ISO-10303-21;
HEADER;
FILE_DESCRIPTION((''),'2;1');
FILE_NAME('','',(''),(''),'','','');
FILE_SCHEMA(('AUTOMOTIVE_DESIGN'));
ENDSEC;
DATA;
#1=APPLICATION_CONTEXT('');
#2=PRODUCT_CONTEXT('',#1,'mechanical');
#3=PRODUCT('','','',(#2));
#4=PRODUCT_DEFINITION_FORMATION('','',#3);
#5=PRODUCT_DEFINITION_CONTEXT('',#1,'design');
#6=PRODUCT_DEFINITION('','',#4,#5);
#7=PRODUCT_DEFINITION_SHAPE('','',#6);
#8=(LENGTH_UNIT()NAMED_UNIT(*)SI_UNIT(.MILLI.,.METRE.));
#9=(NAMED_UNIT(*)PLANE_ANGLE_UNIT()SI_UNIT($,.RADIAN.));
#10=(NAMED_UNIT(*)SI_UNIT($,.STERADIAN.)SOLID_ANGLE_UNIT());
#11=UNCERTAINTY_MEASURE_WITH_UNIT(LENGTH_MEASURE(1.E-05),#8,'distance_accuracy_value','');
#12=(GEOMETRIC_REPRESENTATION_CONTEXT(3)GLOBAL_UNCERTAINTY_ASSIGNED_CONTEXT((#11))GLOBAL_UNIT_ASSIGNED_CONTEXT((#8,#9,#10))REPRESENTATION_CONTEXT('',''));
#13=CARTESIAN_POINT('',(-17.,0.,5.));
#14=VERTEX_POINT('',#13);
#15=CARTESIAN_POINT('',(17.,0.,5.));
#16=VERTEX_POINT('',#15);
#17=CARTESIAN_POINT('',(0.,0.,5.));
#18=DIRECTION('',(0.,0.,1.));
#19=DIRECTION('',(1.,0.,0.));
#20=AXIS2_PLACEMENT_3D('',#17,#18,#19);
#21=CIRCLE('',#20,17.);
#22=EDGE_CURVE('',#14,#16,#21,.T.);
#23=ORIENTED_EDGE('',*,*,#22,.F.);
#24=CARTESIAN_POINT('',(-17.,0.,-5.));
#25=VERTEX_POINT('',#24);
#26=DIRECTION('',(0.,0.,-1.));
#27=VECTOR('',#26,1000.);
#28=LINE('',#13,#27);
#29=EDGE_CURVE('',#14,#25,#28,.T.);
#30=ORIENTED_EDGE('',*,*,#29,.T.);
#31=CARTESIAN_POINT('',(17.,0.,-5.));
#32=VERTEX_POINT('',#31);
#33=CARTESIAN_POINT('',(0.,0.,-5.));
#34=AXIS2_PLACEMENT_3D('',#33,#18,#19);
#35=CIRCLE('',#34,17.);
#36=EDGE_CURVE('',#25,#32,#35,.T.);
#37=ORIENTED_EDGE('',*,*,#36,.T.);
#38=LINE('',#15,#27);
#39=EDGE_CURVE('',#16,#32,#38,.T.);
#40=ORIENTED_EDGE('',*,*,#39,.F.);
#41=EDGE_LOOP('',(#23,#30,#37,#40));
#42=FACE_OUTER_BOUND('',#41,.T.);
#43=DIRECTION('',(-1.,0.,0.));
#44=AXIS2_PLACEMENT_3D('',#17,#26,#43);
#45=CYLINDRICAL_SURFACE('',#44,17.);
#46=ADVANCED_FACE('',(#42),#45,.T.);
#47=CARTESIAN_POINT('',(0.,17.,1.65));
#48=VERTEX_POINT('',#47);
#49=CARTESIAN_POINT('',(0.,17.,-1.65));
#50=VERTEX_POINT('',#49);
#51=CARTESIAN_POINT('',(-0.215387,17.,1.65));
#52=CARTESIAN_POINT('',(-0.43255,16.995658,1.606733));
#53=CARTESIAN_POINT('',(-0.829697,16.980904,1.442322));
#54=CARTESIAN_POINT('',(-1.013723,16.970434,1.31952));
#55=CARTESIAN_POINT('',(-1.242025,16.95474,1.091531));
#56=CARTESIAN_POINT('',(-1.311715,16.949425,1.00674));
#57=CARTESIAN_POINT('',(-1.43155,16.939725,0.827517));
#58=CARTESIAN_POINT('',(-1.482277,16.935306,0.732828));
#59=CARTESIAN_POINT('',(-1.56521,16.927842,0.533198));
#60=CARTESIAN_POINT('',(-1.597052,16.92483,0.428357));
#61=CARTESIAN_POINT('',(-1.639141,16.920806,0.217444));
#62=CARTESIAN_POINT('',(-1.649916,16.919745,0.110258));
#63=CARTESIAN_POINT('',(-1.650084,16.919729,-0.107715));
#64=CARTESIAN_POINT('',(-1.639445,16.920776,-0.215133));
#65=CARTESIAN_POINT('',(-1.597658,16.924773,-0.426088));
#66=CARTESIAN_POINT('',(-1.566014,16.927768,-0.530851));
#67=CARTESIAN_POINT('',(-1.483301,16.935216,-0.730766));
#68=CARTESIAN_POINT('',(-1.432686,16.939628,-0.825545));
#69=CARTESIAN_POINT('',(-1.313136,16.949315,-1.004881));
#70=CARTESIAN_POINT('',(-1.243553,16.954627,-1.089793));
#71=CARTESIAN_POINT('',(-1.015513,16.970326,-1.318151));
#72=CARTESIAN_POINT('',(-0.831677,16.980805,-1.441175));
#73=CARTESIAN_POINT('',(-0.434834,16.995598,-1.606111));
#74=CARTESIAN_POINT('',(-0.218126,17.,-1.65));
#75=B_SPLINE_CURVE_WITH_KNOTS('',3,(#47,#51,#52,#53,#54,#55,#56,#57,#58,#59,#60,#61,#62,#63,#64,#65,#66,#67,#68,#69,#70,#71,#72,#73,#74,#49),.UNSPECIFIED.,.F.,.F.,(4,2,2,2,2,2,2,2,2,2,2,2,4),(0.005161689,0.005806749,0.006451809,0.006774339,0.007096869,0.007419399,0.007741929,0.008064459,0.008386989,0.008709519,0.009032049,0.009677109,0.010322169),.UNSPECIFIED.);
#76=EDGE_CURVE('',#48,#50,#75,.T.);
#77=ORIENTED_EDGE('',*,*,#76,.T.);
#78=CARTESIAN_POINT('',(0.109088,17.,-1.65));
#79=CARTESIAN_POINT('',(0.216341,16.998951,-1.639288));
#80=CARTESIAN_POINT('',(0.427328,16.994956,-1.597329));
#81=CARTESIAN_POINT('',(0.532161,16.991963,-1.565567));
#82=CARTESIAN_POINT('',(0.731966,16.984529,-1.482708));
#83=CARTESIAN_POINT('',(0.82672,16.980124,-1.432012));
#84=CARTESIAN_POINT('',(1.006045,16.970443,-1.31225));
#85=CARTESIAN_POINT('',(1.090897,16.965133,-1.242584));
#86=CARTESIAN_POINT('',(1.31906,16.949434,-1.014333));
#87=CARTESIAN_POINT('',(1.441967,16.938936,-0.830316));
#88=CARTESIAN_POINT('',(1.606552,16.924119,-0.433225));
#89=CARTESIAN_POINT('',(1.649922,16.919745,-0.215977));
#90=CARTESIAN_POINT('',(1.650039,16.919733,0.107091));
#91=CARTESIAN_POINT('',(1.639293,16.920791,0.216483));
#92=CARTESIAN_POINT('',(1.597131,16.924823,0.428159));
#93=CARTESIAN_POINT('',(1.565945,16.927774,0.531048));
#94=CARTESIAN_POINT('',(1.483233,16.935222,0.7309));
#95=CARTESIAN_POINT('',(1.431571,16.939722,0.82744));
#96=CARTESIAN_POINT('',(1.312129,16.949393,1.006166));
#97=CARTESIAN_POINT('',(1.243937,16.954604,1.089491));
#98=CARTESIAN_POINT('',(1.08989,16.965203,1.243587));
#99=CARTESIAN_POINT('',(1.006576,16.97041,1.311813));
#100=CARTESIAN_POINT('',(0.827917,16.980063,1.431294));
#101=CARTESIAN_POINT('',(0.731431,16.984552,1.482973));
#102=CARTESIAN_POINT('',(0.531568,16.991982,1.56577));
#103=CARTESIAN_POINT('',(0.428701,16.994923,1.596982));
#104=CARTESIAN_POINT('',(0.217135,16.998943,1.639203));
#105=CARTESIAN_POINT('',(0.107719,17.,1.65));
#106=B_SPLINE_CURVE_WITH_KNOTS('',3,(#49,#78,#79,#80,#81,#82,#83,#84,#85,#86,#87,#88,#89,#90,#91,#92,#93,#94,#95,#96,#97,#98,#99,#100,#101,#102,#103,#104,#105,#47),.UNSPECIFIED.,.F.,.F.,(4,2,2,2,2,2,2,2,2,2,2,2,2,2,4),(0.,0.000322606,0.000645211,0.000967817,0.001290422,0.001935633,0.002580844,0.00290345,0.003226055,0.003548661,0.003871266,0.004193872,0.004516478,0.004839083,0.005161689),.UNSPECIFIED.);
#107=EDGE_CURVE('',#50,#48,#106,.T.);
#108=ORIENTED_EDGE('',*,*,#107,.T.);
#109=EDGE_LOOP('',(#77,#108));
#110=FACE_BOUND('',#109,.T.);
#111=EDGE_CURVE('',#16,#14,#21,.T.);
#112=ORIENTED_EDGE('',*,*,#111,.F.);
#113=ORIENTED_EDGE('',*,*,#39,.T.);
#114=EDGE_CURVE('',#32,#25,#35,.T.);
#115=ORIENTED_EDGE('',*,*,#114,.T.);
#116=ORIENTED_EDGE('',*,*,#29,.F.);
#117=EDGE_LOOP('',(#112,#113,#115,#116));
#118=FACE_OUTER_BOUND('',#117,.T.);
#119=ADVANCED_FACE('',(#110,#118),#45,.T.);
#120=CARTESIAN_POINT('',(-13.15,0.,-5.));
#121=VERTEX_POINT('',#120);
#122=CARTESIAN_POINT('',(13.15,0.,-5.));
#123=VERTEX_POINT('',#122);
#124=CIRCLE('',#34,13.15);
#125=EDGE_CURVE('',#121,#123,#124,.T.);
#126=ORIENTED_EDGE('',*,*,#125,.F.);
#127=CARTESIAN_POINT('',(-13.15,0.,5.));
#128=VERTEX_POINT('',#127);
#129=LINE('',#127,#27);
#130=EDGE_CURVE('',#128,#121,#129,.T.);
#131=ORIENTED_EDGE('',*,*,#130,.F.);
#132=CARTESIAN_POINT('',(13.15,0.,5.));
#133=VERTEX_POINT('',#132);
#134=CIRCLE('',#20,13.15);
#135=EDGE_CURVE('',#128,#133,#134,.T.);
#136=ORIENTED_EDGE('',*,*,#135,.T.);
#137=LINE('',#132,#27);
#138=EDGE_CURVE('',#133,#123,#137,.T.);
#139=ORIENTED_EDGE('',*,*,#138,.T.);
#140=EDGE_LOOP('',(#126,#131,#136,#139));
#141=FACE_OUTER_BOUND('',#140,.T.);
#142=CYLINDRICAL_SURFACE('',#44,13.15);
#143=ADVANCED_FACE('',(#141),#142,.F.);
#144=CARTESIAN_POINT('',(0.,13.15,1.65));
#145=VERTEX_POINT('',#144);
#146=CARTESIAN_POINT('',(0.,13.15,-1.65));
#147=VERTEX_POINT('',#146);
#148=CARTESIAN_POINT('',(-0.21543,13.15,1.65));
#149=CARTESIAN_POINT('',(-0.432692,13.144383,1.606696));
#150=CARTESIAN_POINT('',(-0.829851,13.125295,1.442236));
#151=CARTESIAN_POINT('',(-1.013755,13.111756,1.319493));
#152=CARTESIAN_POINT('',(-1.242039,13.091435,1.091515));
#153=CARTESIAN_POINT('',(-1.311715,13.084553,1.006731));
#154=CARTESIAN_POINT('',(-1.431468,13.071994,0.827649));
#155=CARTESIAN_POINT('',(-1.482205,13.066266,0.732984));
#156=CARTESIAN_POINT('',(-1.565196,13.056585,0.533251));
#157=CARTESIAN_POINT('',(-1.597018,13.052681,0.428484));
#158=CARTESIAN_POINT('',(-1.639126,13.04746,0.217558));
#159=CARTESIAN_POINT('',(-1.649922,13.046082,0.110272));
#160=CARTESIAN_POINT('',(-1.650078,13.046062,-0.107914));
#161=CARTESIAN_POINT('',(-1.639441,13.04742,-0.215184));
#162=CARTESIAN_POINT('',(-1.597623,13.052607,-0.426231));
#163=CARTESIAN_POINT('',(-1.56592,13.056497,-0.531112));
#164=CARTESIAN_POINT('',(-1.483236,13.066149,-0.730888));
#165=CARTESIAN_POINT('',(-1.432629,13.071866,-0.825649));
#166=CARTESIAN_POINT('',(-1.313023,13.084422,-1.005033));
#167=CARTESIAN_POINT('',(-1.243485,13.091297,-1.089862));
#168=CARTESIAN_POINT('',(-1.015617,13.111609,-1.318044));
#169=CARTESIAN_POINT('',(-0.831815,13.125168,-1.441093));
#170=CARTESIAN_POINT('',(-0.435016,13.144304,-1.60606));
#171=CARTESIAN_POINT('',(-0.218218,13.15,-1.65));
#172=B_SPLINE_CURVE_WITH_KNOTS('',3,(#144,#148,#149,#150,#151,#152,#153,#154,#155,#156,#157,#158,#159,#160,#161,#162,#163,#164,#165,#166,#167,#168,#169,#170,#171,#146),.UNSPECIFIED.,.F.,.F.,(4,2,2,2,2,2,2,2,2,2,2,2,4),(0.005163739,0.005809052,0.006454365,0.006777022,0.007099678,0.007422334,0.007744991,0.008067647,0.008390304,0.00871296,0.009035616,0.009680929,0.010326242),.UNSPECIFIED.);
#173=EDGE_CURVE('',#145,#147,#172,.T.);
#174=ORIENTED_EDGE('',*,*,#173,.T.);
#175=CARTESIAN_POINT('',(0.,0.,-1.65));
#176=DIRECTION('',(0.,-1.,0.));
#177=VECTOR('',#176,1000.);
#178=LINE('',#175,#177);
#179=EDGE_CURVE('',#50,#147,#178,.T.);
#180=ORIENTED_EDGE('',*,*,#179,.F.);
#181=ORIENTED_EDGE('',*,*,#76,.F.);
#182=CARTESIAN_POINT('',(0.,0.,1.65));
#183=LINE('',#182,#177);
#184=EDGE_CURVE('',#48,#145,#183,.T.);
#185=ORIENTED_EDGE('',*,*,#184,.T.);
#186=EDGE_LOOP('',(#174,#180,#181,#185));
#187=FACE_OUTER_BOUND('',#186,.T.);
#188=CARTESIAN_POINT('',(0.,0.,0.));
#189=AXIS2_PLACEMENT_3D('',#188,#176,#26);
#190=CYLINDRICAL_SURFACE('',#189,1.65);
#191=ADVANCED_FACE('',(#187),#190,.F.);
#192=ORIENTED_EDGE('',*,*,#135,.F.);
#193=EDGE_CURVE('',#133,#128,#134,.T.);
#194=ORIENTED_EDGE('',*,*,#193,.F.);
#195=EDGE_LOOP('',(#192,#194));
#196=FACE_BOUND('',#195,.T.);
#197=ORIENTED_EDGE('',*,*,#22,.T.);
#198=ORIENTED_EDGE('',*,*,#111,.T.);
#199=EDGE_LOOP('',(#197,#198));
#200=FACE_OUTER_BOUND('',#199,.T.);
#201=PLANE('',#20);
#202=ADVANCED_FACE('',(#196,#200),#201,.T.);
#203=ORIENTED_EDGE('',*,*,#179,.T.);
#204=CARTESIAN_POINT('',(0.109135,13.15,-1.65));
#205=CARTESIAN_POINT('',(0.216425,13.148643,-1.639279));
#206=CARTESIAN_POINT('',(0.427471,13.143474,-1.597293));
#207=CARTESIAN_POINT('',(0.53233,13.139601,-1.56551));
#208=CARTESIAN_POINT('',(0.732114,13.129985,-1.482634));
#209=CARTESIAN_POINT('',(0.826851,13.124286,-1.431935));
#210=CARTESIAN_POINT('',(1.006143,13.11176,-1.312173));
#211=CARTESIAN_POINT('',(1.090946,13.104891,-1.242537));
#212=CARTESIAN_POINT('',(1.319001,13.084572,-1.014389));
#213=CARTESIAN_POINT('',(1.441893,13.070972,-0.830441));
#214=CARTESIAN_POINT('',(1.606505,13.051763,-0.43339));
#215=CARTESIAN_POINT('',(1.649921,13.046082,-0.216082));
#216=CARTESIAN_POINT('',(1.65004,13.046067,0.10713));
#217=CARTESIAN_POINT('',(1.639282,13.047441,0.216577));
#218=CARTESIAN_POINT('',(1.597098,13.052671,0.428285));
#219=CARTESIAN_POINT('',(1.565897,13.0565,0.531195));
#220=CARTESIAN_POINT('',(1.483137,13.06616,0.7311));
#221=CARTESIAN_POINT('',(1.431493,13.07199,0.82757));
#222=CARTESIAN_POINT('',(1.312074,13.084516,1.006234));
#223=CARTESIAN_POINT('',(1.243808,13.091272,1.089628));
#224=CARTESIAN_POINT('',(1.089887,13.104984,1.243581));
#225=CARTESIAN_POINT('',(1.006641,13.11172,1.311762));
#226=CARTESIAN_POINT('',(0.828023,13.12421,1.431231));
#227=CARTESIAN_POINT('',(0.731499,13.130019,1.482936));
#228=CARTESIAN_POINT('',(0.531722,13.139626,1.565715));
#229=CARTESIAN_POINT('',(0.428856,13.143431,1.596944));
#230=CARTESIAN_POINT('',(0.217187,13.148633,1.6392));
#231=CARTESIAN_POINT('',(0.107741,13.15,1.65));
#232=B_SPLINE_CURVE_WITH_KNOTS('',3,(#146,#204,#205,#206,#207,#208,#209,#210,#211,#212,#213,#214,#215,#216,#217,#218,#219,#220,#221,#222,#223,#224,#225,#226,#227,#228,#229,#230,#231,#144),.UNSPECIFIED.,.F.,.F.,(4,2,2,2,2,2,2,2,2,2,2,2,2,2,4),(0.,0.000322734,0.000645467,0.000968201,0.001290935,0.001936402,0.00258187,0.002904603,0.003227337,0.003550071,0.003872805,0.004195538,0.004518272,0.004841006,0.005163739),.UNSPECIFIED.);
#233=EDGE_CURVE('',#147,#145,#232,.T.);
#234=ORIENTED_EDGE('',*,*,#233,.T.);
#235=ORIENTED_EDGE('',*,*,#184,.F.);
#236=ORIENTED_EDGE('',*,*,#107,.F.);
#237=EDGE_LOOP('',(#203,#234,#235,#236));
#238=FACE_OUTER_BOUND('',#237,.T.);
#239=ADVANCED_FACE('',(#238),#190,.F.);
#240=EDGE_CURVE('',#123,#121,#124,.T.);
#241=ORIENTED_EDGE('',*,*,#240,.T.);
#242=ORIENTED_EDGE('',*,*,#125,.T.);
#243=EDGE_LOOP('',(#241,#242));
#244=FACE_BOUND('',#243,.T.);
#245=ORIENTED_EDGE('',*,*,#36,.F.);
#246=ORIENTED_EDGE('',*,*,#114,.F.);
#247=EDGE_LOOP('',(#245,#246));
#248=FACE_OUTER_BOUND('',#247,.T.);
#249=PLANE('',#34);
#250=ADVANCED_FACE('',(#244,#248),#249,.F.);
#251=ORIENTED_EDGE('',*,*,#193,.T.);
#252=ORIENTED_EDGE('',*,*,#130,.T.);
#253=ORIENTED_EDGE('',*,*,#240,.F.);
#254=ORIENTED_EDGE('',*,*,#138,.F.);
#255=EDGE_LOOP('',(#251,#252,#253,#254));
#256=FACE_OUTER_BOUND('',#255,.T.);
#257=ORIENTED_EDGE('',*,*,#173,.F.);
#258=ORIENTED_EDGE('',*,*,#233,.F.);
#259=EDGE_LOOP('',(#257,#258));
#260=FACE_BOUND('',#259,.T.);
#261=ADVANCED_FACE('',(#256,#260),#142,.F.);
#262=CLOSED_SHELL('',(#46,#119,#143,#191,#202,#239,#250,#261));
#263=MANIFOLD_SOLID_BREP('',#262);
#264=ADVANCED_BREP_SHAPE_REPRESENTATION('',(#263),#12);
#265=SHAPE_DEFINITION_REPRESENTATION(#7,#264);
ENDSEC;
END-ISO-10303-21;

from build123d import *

# Parameters (mm, degrees)
SKETCH_1_R      = 17
SKETCH_1_R_2    = 13.15
EXTRUDE_1_DEPTH = 5
SKETCH_8_W      = 1.65
SKETCH_8_H      = 17


with BuildPart() as part:
    # 草图1 → 凸台-拉伸1 (new, symmetric)
    with BuildSketch(Plane.XY):
        Circle(SKETCH_1_R)
        Circle(SKETCH_1_R_2, mode=Mode.SUBTRACT)
    extrude(amount=EXTRUDE_1_DEPTH, both=True)

    # 草图8 → M4 螺纹孔2 (revolve, cut)
    with BuildSketch(Plane(origin=(0, 0, 0), x_dir=(0, 0, -1), z_dir=(1, 0, 0))):
        with Locations((0.825, 8.5)):
            Rectangle(SKETCH_8_W, SKETCH_8_H)
    revolve(axis=Axis((0, -6.35, 0), (0, 1, 0)), mode=Mode.SUBTRACT)


solid = part.part
